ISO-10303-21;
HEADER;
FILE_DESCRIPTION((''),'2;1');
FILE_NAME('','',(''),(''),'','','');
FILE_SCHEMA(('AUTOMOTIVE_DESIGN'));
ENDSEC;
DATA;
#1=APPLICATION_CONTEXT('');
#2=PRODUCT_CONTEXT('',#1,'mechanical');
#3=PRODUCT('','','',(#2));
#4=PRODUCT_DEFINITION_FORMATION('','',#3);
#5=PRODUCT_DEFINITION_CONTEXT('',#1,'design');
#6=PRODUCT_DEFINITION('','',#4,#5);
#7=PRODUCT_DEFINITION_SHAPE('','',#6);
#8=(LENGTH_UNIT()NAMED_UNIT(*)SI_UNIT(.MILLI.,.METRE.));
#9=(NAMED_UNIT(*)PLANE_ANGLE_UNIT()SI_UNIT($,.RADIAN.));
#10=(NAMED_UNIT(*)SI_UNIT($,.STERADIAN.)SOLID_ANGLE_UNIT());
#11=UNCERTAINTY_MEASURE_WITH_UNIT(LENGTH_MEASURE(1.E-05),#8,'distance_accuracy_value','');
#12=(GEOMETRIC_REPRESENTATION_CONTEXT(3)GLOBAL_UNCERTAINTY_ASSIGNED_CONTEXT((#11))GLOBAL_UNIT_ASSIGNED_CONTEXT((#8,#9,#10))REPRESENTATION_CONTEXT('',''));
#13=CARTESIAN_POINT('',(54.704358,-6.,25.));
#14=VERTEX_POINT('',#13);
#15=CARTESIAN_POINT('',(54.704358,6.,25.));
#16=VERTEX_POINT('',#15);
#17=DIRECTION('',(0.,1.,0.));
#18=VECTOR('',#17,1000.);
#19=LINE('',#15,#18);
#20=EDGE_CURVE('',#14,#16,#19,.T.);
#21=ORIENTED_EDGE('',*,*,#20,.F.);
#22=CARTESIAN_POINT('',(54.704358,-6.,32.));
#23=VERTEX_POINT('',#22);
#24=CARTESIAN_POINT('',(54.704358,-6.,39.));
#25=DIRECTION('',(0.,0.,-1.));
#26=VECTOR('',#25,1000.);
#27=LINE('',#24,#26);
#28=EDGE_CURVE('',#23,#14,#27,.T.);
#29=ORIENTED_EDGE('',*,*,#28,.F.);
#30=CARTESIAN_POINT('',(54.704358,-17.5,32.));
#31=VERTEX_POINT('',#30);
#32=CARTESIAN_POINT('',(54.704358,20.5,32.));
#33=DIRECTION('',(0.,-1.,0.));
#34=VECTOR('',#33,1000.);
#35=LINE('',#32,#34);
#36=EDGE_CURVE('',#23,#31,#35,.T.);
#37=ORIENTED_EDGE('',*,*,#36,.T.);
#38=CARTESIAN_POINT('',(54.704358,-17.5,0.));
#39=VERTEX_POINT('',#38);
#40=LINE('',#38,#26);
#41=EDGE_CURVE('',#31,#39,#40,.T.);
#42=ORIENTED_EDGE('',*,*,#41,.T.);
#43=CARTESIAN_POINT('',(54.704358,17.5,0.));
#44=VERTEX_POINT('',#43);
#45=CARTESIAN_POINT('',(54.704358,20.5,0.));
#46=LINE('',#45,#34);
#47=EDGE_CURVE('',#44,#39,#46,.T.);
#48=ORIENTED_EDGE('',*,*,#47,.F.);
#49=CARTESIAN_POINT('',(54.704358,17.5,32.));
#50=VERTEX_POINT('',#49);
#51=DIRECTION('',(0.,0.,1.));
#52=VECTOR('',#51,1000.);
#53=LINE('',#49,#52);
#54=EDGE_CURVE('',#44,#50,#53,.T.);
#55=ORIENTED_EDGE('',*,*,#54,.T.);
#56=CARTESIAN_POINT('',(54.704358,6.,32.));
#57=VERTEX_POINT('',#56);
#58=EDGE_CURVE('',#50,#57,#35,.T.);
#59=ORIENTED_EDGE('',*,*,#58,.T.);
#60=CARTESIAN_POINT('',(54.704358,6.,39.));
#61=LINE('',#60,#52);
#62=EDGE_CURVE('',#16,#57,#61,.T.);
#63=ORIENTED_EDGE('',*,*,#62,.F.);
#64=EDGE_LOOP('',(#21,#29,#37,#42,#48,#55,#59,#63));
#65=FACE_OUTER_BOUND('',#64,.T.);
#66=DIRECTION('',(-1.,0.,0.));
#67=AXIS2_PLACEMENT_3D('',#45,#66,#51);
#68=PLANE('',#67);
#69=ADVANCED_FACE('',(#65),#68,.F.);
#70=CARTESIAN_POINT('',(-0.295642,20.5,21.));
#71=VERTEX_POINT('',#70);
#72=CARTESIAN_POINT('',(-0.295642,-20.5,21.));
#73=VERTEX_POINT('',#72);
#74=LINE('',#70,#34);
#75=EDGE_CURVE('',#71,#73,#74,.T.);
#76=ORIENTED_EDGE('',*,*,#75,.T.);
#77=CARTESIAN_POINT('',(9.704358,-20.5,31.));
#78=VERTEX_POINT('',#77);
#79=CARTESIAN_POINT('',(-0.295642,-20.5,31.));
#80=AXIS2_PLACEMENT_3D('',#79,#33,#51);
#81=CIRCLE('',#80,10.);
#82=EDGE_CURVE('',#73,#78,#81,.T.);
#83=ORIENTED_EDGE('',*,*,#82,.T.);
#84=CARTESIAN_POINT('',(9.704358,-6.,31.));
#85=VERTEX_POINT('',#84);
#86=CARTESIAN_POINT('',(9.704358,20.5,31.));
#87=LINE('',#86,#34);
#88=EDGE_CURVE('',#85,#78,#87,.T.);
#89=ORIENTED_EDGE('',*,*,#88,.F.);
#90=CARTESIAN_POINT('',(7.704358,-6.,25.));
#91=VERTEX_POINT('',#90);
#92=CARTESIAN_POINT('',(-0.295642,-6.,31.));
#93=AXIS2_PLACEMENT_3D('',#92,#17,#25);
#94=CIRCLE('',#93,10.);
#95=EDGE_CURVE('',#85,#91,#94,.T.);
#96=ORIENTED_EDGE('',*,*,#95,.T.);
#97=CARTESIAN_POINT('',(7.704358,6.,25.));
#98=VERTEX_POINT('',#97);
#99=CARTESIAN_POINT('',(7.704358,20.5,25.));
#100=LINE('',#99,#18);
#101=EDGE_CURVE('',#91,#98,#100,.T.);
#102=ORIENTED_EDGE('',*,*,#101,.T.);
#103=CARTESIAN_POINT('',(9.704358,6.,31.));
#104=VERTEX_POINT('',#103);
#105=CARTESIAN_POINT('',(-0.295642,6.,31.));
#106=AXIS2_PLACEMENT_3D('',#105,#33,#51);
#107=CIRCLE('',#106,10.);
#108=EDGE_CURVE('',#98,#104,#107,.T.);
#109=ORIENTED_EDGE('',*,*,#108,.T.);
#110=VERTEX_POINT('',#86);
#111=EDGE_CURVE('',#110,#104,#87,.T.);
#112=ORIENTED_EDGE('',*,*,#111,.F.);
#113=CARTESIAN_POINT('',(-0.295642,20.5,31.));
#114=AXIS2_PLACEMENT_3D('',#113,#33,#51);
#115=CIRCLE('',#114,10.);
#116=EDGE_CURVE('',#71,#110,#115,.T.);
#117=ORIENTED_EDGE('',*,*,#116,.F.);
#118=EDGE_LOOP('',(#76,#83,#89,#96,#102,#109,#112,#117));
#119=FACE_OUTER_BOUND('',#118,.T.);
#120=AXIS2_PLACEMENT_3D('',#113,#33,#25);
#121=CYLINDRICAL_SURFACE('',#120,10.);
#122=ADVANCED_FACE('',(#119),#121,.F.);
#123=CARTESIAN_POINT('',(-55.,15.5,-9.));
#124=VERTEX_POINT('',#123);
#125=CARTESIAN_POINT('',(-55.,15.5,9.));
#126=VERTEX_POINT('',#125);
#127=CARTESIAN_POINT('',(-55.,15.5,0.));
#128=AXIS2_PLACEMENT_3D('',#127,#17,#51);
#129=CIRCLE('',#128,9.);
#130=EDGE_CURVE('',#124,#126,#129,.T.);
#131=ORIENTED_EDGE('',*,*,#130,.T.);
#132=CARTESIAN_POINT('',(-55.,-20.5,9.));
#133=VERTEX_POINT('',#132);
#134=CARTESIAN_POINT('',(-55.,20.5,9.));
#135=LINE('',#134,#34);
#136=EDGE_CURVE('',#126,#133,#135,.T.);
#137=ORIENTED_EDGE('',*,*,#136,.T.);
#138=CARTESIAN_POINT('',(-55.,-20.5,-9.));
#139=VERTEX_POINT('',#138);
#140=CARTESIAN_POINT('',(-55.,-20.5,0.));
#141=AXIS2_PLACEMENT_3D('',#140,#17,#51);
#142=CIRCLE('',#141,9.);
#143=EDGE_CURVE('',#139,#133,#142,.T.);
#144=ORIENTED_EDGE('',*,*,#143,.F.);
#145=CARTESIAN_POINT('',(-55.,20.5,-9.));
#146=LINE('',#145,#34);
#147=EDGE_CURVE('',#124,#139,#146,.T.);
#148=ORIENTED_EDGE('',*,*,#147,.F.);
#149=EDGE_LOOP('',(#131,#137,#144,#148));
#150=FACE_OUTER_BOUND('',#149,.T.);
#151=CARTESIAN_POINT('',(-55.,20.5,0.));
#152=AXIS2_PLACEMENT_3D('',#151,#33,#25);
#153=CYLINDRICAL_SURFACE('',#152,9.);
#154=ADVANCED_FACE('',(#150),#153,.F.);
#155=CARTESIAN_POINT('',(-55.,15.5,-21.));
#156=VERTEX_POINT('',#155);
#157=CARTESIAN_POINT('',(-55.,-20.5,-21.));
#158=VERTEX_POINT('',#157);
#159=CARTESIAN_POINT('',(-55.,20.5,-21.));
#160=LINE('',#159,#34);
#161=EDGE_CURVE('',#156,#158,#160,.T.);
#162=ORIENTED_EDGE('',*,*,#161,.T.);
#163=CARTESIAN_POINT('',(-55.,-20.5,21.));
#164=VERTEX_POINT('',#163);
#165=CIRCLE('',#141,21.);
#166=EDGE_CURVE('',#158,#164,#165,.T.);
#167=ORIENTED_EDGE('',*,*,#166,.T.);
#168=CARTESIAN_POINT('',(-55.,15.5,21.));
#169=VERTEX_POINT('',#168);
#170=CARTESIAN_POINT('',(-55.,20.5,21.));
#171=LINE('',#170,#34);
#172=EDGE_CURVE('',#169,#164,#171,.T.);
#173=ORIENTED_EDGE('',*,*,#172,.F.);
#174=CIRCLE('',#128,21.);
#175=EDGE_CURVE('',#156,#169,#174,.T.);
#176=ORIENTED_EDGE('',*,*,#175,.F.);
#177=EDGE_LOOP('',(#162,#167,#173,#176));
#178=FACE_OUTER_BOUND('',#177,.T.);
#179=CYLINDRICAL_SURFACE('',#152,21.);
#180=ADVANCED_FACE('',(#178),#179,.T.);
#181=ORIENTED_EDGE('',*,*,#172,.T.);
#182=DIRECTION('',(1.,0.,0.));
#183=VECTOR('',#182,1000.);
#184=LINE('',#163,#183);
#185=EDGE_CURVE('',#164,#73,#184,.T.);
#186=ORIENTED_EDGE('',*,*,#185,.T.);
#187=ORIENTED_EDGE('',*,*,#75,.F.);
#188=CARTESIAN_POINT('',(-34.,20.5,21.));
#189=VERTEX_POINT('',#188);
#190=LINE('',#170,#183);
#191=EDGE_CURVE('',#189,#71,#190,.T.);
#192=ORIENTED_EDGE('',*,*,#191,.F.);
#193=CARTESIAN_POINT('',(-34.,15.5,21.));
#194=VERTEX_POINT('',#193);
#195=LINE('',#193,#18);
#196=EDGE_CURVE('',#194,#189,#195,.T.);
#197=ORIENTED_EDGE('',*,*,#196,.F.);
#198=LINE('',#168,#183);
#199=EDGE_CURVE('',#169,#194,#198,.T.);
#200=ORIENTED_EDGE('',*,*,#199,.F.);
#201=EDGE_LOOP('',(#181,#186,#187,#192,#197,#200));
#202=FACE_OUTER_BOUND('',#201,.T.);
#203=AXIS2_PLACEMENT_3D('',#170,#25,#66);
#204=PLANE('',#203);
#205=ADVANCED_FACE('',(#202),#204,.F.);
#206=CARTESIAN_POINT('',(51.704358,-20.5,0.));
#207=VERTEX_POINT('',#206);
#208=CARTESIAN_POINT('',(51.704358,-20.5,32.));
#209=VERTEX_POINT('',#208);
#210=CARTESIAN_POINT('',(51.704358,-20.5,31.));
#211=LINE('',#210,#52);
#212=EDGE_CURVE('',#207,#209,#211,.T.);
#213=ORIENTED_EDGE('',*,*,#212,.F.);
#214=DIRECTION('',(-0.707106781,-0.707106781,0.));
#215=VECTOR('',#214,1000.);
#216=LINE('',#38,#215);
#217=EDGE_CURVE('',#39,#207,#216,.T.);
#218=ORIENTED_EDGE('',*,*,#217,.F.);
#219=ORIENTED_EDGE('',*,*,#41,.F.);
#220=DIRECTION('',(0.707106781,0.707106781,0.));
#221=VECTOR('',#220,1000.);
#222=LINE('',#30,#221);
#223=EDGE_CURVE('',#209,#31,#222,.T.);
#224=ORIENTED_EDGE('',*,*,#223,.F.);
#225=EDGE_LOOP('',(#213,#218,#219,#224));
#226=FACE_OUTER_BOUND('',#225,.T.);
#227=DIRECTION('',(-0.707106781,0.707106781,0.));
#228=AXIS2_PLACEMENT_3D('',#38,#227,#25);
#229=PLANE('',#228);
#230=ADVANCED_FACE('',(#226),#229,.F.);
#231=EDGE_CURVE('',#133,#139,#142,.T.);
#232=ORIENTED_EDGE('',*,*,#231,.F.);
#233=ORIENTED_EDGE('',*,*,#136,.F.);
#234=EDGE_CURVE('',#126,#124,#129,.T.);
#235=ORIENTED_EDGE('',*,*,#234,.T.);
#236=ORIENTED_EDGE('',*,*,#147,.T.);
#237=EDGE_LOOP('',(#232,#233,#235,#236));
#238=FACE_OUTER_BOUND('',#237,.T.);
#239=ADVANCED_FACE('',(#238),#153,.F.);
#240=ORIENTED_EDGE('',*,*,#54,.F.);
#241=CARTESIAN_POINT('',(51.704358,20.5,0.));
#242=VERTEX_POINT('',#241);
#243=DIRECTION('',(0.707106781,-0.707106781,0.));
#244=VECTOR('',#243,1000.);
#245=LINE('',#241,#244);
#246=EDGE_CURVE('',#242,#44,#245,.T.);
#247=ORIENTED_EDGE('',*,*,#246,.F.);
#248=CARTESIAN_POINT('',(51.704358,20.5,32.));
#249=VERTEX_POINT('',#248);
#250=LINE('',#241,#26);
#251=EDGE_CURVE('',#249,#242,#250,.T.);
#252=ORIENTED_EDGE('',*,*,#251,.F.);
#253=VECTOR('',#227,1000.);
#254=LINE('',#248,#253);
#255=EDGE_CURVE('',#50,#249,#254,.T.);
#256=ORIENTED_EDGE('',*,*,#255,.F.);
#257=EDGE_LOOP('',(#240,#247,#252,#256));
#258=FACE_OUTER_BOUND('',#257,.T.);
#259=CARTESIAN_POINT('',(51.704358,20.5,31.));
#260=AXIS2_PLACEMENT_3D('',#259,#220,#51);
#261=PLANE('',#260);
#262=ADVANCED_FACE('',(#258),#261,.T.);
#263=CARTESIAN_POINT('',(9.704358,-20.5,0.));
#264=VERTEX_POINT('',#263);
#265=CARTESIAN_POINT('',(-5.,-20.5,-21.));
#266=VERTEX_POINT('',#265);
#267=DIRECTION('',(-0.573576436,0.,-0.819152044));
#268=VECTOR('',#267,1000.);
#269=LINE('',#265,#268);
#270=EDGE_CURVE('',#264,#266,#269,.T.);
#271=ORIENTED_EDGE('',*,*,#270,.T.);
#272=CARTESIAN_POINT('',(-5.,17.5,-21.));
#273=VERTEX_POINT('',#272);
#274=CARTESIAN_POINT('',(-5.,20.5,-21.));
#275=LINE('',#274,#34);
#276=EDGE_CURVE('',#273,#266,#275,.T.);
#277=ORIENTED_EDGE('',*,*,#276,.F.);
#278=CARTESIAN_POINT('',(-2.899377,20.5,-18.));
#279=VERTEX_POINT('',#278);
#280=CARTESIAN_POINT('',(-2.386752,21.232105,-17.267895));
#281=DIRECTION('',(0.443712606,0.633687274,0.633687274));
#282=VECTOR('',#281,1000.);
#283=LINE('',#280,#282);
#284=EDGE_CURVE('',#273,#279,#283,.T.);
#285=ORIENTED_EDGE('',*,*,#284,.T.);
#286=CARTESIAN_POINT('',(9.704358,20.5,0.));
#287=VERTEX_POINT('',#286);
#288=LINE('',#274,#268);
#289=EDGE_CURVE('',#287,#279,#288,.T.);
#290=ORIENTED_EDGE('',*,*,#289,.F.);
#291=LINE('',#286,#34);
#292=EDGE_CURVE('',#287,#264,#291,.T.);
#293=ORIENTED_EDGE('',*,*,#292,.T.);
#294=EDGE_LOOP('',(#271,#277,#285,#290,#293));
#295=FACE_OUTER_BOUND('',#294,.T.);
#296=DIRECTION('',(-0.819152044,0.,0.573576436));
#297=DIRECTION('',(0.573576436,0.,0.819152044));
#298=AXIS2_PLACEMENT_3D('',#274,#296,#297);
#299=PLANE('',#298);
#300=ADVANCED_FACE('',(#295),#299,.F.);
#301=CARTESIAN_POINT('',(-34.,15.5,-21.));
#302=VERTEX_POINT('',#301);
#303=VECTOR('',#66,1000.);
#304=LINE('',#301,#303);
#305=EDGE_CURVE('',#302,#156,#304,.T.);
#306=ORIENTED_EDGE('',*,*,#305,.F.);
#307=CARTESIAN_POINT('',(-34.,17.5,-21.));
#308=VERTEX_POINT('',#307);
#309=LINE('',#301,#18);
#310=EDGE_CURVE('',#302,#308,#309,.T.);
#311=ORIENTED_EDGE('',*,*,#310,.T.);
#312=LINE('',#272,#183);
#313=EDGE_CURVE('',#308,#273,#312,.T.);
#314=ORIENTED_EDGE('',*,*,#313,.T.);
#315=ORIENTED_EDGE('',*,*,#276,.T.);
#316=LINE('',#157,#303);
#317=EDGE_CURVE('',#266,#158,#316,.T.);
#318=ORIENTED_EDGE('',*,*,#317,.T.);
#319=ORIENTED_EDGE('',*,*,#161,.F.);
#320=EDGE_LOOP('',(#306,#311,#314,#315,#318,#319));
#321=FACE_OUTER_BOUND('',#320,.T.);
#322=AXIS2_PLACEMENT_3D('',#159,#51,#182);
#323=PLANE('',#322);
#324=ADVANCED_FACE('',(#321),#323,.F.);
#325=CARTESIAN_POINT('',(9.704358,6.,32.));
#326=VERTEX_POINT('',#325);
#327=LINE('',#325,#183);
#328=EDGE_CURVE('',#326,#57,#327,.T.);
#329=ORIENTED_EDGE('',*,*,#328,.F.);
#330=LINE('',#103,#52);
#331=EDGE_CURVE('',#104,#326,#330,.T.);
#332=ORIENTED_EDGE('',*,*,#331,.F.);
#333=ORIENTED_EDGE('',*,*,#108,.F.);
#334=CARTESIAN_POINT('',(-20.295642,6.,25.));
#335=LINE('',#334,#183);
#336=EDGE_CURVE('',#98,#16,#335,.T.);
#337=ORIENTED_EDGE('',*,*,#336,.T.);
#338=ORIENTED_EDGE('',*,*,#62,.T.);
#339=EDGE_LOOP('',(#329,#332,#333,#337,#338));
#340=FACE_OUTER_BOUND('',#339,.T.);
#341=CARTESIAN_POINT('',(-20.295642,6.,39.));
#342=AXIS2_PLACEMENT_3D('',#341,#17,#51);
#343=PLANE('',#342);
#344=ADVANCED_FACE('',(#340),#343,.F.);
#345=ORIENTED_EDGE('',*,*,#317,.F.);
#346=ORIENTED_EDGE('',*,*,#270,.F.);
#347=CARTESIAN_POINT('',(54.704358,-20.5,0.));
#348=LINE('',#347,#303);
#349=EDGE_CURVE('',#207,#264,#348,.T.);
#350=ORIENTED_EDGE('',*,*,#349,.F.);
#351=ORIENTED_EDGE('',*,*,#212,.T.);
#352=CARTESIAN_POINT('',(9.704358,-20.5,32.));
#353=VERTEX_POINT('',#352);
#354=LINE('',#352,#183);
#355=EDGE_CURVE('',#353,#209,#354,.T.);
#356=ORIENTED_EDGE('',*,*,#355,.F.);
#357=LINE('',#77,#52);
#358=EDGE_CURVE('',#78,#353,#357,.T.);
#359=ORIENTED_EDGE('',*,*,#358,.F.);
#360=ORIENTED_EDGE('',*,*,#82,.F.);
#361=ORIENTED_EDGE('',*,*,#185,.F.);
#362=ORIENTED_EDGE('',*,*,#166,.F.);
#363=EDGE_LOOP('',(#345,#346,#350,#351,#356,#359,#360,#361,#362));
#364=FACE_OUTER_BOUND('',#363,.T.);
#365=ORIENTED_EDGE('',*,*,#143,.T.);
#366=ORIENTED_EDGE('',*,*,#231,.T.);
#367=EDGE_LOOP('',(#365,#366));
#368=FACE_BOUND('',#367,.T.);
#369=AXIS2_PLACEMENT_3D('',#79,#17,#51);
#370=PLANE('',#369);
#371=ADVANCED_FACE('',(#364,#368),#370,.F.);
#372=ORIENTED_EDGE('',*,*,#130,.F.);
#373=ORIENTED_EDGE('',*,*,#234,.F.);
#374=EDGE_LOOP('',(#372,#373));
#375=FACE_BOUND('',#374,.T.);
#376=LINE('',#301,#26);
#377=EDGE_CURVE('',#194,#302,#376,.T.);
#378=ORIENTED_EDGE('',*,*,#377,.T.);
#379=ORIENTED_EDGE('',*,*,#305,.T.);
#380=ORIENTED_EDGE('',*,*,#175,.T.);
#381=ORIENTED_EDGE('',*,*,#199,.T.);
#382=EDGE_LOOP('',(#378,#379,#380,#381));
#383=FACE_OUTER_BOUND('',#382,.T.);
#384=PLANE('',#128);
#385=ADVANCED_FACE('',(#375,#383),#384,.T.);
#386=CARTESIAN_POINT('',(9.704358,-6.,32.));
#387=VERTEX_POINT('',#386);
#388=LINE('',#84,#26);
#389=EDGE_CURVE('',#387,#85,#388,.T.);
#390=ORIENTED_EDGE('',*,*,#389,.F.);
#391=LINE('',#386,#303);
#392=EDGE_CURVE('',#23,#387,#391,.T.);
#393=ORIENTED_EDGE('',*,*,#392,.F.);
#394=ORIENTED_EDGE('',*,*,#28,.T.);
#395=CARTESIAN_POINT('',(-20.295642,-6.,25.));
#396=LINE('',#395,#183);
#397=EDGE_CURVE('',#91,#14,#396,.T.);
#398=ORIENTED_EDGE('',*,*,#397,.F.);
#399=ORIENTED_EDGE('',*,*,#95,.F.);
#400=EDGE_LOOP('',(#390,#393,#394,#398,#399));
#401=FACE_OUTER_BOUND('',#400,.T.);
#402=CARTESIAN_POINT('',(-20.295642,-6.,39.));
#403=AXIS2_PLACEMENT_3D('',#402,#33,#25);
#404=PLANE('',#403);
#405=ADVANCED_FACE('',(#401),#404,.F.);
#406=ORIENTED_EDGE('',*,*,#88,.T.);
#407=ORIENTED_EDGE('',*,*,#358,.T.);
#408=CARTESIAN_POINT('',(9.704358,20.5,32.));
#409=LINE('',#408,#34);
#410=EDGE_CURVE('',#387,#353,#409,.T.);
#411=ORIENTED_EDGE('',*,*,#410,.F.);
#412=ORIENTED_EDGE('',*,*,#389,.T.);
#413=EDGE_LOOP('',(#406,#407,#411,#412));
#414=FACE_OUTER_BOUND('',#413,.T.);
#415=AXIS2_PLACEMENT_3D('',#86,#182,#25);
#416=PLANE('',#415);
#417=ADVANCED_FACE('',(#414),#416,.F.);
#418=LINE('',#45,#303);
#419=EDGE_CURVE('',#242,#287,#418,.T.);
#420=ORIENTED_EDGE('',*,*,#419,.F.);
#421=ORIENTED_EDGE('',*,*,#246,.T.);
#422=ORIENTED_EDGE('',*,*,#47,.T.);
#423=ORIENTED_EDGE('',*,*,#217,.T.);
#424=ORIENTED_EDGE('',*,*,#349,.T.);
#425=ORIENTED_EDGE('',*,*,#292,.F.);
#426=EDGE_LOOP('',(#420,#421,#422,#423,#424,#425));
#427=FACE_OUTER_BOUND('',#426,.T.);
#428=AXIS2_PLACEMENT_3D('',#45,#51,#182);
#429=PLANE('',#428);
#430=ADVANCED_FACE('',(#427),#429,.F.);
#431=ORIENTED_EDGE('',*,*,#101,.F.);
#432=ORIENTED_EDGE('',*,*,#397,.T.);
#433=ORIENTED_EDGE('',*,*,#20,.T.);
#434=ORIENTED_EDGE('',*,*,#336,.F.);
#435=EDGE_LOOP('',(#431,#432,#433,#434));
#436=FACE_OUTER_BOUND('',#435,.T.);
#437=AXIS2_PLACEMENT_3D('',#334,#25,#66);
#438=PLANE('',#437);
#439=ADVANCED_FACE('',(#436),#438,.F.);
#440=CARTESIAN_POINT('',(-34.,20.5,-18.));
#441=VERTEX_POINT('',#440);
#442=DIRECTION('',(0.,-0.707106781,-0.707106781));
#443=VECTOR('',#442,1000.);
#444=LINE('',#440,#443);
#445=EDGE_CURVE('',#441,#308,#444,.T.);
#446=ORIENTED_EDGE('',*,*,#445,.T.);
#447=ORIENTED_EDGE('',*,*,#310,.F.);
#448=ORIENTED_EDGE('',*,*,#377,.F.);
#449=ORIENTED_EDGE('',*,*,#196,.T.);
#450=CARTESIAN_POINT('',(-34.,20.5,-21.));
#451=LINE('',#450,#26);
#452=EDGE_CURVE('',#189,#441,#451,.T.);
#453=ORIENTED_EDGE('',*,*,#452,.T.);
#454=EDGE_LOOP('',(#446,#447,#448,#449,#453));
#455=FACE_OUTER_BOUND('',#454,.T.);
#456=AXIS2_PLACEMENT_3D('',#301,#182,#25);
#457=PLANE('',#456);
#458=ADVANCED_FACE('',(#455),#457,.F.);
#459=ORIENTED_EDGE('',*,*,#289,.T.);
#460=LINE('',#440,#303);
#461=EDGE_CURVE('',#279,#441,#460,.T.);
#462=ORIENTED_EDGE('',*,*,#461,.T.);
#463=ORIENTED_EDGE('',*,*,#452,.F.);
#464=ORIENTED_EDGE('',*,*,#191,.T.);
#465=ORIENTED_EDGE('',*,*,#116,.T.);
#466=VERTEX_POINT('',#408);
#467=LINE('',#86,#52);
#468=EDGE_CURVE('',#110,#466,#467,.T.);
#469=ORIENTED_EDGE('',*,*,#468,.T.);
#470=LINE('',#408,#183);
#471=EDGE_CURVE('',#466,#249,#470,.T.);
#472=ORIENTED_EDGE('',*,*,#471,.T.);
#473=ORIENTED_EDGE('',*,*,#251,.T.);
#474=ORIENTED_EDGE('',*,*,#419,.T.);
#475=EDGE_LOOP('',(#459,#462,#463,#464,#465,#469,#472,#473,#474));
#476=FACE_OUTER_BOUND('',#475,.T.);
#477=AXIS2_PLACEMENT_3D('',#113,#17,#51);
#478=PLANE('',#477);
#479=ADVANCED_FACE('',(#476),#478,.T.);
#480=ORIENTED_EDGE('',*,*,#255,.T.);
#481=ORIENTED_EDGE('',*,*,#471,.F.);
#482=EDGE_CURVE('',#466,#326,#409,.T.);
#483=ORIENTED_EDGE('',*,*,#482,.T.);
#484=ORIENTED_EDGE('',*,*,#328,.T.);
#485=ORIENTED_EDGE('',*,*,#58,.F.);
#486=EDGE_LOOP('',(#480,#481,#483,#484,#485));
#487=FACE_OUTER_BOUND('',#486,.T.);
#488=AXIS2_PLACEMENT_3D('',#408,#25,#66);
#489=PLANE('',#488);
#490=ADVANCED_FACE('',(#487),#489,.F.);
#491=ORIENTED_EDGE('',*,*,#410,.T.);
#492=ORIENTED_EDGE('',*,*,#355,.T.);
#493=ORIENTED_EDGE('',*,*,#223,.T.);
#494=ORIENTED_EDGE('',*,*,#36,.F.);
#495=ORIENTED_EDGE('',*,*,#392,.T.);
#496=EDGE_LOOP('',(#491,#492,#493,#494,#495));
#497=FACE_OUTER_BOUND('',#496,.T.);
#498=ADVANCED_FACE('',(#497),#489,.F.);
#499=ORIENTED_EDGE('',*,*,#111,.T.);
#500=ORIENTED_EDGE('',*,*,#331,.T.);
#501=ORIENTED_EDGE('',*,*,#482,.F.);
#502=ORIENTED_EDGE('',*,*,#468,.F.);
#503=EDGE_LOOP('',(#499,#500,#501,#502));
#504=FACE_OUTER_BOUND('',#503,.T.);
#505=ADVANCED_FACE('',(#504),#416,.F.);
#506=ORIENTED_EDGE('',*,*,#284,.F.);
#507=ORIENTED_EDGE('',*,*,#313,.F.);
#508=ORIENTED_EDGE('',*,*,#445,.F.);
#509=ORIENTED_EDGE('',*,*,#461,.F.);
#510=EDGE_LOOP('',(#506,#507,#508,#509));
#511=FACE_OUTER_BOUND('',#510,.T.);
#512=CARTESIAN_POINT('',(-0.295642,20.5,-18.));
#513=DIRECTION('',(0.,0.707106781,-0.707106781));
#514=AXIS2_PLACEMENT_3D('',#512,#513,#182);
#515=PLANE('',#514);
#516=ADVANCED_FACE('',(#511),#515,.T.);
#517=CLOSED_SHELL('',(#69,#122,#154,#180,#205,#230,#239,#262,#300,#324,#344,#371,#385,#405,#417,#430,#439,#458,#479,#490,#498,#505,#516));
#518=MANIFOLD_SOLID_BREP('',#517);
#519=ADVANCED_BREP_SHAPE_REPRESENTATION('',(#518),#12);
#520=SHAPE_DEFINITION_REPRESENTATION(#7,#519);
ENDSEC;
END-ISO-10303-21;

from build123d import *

# Parameters (mm, degrees)
LINK_PROFILE_SKETCH_R    = 9
LINK_BODY_DEPTH          = 20.5
EYE_RECESS_CUT_5MM_DEPTH = 5
SLOT_SKETCH_W            = 14
SLOT_SKETCH_H            = 12
SLOT_CUT_14X12_DEPTH     = 75
END_CHAMFER_3MM_SIZE     = 3


with BuildPart() as part:
    # Link Profile Sketch → Link Body (new, symmetric)
    with BuildSketch(Plane(origin=(0, 0, 0), x_dir=(1, 0, 0), z_dir=(0, 1, 0))):
        with BuildLine():
            Line((9.704358302, -32), (54.704358302, -32))
            Line((54.704358302, -32), (54.704358302, 0))
            Line((54.704358302, 0), (9.704358302, 0))
            Line((9.704358302, 0), (-5, 21))
            Line((-5, 21), (-55, 21))
            ThreePointArc((-55, 21), (-76, 0), (-55, -21))
            Line((-55, -21), (-0.295641698, -21))
            ThreePointArc((-0.295641698, -21), (6.775426114, -23.928932188), (9.704358302, -31))
            Line((9.704358302, -31), (9.704358302, -32))
        make_face()
        with Locations(Location((-55, 0, 0), (0, 0, 270))):
            Circle(LINK_PROFILE_SKETCH_R, mode=Mode.SUBTRACT)
    extrude(amount=LINK_BODY_DEPTH, both=True)

    # Eye Recess Sketch → Eye Recess Cut 5mm (cut)
    with BuildSketch(Plane(origin=(0, 20.5, 0), x_dir=(1, 0, 0), z_dir=(0, 1, 0))):
        with BuildLine():
            Line((-55, -21), (-34, -21))
            Line((-34, -21), (-34, 21))
            Line((-34, 21), (-55, 21))
            ThreePointArc((-55, 21), (-76, 0), (-55, -21))
        make_face()
    extrude(amount=-EYE_RECESS_CUT_5MM_DEPTH, mode=Mode.SUBTRACT)

    # Slot Sketch → Slot Cut 14x12 (cut)
    with BuildSketch(Plane(origin=(54.704358302, 0, 0), x_dir=(0, 0, -1), z_dir=(1, 0, 0))):
        with Locations((-32, 0)):
            Rectangle(SLOT_SKETCH_W, SLOT_SKETCH_H)
    extrude(amount=-SLOT_CUT_14X12_DEPTH, mode=Mode.SUBTRACT)

    # End Chamfer 3mm
    end_chamfer_3mm_edges = [part.edges().sort_by_distance(p)[0] for p in [
        (54.704358302, -20.5, 16),
        (-19.5, 20.5, -21),
        (54.704358302, 20.5, 16),
    ]]
    chamfer(end_chamfer_3mm_edges, length=END_CHAMFER_3MM_SIZE)


solid = part.part
